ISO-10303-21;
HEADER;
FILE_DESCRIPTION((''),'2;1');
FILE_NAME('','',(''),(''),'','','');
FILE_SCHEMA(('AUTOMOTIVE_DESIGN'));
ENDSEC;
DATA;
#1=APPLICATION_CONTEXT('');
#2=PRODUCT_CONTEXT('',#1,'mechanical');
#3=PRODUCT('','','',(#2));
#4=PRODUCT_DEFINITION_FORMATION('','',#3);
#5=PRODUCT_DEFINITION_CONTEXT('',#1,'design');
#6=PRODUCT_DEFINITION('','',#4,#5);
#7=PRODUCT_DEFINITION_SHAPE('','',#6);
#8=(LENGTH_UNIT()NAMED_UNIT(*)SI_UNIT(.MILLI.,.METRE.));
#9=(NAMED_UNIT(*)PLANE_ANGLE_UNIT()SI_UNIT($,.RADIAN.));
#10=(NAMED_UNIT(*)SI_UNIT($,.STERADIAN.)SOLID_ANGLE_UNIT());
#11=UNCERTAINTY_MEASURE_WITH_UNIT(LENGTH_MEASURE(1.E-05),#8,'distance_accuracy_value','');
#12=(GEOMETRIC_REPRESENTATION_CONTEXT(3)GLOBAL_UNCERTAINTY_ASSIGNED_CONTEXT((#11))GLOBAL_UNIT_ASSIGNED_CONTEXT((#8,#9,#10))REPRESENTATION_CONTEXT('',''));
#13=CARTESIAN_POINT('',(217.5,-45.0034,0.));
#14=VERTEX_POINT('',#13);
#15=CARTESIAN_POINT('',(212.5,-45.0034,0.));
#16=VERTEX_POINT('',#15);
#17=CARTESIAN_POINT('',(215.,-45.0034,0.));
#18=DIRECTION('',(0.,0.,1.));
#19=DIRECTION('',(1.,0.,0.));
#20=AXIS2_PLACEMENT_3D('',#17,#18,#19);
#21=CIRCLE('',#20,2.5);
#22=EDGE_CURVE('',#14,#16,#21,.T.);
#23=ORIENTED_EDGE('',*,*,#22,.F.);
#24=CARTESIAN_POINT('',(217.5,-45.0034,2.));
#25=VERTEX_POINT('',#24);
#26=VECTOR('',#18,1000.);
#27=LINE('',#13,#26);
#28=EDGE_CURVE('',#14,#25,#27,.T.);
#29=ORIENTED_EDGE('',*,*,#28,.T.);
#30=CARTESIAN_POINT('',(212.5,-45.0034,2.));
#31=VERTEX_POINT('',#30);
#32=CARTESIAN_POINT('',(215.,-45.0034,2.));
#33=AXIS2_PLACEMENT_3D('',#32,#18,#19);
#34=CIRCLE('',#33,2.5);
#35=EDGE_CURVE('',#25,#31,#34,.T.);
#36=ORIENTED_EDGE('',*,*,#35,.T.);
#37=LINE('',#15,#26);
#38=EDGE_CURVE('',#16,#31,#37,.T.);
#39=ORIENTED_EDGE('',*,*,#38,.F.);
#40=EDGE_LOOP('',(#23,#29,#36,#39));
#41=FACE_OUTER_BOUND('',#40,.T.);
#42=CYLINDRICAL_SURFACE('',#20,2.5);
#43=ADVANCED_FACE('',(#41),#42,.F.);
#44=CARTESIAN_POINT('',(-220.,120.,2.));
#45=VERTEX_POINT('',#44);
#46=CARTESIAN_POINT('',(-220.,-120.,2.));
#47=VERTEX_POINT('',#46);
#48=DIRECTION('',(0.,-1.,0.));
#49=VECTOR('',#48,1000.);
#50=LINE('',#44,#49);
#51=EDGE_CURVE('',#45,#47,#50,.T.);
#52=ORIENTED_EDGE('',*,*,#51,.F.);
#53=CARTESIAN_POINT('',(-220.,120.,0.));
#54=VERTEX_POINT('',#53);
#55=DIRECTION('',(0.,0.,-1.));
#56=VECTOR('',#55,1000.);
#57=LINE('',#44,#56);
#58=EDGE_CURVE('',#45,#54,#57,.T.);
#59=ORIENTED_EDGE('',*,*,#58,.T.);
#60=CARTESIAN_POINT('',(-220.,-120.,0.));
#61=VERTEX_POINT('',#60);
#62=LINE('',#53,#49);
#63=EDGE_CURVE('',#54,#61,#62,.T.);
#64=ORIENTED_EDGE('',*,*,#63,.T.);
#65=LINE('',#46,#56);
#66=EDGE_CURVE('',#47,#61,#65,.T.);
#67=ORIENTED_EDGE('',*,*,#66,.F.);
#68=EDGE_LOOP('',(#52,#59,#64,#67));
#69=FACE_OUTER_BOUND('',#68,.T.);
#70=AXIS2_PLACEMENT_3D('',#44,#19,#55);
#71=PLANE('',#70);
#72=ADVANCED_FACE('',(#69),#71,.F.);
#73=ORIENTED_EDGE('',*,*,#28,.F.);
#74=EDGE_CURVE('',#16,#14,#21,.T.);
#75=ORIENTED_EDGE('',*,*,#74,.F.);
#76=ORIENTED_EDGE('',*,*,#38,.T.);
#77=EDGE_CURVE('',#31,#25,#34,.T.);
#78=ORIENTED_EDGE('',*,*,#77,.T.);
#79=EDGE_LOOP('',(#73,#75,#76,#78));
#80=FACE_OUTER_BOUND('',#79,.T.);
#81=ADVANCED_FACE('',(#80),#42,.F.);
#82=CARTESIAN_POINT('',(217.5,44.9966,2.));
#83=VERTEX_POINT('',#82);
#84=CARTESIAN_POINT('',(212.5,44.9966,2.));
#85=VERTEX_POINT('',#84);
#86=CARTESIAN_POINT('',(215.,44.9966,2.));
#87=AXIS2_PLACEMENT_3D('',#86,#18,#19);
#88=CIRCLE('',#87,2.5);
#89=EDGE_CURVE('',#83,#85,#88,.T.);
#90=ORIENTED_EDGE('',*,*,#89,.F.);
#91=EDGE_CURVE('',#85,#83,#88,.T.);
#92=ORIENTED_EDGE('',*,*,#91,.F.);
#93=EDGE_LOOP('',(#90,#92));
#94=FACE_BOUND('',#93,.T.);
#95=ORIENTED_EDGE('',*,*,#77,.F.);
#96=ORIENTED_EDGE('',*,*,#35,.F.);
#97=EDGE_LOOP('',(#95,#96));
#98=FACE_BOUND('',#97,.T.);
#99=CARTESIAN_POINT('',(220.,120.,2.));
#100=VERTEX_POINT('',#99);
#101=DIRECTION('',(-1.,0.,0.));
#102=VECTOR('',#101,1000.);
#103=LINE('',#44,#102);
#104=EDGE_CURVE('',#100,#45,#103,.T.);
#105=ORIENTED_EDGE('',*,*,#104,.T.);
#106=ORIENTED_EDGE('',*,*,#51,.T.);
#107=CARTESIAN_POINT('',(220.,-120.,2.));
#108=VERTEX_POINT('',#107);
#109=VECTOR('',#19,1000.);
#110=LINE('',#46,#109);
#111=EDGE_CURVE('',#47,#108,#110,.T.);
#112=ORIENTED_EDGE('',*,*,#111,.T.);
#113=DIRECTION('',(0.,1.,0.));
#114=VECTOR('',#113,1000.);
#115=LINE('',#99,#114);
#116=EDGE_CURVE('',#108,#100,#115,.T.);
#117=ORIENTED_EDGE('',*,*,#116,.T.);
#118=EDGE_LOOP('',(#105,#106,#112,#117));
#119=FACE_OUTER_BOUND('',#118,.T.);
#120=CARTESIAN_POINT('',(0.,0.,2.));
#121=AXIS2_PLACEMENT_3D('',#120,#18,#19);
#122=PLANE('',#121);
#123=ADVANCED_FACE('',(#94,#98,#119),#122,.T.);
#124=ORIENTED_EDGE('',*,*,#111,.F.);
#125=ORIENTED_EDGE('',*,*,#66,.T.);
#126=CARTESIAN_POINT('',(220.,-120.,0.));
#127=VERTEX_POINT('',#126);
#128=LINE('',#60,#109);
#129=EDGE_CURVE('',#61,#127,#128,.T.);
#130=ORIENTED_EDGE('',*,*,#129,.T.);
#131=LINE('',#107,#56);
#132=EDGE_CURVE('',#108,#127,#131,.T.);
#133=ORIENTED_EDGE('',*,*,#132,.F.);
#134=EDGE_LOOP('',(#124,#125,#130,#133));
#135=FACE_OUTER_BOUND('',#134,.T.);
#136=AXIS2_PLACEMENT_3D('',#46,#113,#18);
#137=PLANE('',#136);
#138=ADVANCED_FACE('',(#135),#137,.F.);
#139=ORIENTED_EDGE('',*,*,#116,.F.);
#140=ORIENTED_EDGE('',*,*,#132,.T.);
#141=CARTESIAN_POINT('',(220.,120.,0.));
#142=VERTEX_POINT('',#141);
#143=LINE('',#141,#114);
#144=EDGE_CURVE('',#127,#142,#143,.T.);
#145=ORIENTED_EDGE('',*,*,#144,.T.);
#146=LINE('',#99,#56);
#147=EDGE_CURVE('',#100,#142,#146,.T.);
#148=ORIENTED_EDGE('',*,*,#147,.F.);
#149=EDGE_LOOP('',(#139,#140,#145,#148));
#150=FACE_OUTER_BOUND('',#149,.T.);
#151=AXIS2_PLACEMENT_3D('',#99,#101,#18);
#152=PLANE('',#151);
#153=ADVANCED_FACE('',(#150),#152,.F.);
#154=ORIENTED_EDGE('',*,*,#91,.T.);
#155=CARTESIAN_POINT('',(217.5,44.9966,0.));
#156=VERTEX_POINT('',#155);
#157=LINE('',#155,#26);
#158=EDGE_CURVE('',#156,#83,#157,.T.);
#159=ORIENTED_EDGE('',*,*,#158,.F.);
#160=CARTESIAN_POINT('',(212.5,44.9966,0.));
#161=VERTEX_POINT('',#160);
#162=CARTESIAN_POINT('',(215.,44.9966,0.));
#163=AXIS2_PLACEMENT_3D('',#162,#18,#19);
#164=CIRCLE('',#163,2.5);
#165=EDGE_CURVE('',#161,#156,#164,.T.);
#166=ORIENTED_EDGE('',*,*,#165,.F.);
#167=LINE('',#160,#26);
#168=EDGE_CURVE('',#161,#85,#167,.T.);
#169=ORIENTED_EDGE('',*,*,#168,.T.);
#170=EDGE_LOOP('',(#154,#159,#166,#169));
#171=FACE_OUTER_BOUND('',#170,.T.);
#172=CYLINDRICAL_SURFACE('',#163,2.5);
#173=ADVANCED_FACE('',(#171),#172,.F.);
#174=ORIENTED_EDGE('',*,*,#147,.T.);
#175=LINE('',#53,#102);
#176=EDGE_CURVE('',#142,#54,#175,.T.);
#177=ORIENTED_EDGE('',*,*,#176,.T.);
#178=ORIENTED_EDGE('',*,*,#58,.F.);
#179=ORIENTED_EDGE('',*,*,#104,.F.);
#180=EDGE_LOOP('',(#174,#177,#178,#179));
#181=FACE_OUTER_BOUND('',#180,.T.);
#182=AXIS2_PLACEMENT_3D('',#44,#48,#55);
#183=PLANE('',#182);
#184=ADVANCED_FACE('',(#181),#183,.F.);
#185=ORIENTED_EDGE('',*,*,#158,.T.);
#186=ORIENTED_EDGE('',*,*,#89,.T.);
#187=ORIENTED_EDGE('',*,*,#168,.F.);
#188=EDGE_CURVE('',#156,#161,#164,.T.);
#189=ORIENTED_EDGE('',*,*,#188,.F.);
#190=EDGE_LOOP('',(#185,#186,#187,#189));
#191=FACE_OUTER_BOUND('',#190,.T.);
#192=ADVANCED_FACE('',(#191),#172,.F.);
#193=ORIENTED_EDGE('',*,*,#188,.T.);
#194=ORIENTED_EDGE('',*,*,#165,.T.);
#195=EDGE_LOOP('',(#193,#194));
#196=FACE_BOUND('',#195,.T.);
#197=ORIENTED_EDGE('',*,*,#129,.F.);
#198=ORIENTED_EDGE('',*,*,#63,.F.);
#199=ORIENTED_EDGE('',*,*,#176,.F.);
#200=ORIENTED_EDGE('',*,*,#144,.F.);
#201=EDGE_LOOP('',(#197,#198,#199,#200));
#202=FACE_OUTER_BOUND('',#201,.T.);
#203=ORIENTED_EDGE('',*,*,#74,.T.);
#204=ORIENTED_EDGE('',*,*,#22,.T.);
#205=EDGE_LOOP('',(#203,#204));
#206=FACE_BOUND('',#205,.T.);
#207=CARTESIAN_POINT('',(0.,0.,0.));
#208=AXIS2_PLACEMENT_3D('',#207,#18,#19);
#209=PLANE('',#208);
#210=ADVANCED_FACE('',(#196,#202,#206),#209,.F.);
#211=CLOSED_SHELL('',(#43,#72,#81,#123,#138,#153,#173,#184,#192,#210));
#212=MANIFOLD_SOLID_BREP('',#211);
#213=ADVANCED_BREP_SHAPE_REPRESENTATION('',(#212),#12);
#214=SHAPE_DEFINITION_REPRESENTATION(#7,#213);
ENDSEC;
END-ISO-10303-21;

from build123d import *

# Parameters (mm, degrees)
SKETCH_1_W          = 440
SKETCH_1_H          = 240
EXTRUDE_1_DEPTH     = 2
SKETCH_2_R          = 2.5
CUT_EXTRUDE_1_DEPTH = 2


with BuildPart() as part:
    # 草图1 → 凸台-拉伸1 (new body)
    with BuildSketch(Plane.XY):
        Rectangle(SKETCH_1_W, SKETCH_1_H)
    extrude(amount=EXTRUDE_1_DEPTH)

    # 草图2 → 切除-拉伸1 (cut)
    with BuildSketch(Plane.XY.offset(2)):
        with Locations((215, 44.9966)):
            Circle(SKETCH_2_R)
        with Locations((215, -45.0034)):
            Circle(SKETCH_2_R)
    extrude(amount=-CUT_EXTRUDE_1_DEPTH, mode=Mode.SUBTRACT)


solid = part.part
